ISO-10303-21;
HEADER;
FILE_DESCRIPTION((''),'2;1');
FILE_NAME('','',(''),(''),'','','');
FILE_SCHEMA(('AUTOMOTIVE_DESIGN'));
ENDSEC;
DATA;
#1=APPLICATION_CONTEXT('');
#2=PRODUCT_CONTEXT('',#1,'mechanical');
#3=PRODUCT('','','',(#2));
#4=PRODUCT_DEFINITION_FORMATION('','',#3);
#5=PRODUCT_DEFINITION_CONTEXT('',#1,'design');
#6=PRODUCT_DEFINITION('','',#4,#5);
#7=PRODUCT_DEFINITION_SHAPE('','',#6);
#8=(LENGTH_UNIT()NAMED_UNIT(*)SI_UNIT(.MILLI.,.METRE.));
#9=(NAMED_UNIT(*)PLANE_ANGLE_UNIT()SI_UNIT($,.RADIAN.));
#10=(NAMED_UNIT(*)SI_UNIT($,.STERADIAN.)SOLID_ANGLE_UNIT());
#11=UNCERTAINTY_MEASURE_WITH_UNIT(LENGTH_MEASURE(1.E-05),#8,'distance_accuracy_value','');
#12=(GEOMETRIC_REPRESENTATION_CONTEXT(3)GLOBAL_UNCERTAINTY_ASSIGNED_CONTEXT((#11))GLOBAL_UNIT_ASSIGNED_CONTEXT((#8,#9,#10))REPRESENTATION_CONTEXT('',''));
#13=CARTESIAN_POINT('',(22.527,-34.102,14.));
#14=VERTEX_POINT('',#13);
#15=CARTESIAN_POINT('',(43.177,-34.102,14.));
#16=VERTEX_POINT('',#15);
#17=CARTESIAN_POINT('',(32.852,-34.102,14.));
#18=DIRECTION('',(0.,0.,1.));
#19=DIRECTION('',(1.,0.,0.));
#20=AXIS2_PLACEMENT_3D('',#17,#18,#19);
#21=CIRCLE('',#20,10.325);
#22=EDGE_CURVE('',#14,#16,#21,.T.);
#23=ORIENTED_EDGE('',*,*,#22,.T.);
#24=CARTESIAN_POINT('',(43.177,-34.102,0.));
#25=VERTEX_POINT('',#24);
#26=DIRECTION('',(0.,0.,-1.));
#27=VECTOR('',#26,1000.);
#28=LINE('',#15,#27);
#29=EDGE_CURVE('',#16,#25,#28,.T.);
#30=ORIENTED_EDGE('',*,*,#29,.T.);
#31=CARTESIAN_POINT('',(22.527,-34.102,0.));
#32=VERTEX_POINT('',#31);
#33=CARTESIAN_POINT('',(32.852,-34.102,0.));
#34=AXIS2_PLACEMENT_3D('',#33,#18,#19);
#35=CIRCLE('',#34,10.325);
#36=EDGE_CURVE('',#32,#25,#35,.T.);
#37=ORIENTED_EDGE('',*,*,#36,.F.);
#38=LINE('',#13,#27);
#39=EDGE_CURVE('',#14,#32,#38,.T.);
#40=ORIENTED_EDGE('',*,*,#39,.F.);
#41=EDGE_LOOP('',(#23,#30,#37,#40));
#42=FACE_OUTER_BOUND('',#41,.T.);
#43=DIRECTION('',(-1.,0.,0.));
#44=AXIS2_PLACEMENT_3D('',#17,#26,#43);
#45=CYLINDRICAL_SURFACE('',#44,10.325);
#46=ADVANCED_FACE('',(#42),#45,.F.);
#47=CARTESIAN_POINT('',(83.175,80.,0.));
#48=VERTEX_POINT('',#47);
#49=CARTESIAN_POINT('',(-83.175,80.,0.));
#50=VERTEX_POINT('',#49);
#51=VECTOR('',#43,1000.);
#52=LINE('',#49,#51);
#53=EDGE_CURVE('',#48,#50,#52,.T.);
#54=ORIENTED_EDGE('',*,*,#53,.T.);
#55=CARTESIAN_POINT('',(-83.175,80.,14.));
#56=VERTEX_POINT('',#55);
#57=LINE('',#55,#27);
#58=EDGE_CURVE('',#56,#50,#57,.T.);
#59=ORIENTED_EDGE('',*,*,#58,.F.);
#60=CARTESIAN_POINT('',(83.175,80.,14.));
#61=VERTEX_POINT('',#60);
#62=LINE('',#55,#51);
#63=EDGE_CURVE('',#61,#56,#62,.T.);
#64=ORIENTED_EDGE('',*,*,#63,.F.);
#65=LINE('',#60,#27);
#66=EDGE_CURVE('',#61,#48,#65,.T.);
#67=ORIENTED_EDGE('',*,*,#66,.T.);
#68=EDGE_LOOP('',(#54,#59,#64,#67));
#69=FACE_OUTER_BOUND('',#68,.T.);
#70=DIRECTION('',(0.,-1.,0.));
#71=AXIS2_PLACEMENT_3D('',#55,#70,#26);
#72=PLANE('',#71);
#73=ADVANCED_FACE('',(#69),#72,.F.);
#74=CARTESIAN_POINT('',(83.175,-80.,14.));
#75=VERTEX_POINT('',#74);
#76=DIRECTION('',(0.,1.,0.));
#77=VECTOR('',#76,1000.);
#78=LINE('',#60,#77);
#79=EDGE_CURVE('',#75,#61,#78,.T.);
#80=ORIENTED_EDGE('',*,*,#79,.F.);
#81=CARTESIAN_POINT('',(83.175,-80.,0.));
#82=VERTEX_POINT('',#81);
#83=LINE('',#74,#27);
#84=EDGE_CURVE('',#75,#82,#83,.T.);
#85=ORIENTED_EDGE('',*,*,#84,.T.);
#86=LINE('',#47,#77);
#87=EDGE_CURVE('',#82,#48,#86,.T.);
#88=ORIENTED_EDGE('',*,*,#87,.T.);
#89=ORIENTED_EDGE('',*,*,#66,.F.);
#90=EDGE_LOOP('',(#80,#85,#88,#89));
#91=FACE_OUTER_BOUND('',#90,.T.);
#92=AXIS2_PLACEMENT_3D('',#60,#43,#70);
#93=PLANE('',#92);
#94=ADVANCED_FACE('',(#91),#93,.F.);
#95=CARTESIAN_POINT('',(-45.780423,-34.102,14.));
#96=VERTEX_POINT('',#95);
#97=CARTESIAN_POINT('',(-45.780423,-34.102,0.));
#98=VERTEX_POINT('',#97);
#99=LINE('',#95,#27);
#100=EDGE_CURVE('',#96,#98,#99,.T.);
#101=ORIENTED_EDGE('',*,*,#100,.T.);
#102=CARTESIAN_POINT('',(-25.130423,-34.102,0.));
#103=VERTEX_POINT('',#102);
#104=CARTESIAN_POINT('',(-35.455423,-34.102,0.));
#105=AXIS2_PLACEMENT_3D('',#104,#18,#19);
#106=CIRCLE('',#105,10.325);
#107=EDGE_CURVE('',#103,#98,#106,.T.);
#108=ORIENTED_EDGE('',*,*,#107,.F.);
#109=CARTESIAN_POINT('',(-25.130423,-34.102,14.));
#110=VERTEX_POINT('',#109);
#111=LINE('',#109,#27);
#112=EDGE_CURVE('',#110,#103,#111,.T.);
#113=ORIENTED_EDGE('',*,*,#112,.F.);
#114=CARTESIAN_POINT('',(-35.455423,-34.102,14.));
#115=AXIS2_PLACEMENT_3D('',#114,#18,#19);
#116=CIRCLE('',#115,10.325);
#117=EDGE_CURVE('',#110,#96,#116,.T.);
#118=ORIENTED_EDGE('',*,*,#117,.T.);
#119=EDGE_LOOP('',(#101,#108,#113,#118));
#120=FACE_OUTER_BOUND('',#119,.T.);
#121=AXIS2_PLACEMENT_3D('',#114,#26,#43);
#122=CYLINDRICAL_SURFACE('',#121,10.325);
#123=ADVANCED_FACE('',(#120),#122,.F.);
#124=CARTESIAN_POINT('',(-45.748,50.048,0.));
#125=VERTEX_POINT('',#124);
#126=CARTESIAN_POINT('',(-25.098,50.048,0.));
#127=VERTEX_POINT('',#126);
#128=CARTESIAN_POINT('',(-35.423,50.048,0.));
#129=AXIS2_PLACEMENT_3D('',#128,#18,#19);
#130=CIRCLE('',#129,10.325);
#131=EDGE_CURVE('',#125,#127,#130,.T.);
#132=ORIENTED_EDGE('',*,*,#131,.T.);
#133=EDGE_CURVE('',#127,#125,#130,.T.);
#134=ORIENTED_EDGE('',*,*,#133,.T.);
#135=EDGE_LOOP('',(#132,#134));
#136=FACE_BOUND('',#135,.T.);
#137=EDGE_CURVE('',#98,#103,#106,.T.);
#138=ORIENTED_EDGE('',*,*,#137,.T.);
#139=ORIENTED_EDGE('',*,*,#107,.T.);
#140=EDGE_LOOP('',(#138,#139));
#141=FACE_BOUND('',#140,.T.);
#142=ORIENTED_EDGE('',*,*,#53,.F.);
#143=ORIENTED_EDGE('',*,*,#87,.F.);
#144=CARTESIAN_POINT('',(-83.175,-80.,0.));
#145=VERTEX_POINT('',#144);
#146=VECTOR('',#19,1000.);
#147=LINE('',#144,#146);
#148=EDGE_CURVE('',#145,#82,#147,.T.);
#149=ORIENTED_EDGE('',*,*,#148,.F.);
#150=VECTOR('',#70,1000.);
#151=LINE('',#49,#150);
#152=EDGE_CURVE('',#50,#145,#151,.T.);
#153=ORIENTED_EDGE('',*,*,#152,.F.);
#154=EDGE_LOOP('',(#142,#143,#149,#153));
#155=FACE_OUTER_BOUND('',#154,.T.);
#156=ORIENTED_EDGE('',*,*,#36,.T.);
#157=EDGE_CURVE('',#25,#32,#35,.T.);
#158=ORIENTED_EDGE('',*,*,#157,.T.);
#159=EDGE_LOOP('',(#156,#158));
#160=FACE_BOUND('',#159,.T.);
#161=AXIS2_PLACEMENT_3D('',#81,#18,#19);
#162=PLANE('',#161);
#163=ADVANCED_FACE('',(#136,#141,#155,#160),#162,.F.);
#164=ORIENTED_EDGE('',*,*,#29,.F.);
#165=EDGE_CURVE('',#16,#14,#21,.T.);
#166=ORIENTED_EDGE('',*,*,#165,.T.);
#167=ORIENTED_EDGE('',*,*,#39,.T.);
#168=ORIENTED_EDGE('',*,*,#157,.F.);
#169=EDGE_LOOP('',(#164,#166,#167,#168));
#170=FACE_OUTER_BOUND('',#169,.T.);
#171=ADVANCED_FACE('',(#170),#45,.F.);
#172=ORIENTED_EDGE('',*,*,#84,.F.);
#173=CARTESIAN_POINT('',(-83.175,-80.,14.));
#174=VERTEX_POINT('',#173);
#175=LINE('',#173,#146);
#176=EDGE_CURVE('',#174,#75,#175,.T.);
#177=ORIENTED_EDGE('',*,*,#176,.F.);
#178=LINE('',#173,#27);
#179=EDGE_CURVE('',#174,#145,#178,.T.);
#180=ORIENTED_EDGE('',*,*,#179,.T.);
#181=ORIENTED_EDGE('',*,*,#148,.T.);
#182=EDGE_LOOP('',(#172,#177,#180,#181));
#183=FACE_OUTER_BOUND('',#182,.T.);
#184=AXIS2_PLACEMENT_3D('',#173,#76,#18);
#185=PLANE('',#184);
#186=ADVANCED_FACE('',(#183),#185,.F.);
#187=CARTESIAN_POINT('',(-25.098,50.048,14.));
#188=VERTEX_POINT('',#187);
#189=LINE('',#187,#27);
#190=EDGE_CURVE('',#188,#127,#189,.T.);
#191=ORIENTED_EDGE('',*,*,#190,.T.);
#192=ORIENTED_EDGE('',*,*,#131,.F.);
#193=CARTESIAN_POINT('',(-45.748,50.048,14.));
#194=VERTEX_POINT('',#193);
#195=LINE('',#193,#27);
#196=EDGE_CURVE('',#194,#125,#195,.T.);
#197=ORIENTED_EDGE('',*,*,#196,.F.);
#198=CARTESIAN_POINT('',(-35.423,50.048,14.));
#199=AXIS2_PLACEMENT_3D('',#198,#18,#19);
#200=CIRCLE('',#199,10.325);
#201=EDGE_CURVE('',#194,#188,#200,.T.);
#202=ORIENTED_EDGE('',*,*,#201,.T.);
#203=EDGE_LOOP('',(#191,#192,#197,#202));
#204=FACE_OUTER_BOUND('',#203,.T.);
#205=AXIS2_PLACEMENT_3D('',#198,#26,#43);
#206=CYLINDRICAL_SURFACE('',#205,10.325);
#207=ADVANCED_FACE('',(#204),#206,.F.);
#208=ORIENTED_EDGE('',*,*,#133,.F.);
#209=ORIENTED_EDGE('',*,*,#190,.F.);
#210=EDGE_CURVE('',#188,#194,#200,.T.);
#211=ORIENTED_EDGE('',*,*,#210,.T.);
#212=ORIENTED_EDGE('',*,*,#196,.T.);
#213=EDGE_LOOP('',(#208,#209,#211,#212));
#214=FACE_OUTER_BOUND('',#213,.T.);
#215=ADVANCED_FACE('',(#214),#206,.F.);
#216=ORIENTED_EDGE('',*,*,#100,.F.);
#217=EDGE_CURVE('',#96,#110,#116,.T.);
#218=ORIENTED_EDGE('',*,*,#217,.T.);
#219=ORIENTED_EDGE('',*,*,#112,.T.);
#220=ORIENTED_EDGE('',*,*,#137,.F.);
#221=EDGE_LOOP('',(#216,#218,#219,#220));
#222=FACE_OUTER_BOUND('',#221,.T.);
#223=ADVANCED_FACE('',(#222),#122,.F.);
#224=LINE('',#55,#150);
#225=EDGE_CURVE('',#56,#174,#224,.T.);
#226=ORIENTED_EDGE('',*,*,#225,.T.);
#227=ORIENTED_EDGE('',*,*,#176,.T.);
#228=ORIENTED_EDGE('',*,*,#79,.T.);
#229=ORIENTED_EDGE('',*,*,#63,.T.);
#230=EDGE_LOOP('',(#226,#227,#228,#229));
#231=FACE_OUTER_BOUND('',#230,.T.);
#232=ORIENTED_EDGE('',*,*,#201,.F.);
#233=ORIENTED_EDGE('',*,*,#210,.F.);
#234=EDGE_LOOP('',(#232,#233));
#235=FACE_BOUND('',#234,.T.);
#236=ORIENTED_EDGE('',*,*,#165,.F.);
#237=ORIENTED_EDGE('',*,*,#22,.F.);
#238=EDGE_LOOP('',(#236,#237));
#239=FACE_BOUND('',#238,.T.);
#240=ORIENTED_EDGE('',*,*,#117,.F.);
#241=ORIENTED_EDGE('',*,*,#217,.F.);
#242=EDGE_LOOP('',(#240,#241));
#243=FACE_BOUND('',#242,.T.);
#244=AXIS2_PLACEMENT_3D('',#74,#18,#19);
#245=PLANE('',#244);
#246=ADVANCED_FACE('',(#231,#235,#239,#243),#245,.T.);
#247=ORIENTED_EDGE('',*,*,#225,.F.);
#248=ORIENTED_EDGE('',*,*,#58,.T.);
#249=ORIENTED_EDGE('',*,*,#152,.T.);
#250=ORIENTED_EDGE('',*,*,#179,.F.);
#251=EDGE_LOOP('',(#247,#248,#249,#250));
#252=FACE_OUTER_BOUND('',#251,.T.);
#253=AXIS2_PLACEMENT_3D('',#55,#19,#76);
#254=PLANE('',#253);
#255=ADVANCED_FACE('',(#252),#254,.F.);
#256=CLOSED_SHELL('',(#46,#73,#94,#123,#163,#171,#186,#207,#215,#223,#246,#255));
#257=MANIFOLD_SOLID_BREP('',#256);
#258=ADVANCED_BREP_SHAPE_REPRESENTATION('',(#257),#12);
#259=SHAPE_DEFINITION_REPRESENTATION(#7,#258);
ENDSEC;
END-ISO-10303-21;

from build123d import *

# Parameters (mm, degrees)
SKETCH1_W           = 166.35
SKETCH1_H           = 160
SKETCH1_R           = 10.325
BOSS_EXTRUDE1_DEPTH = 14


with BuildPart() as part:
    # Sketch1 → Boss-Extrude1 (new body)
    with BuildSketch(Plane.XY):
        Rectangle(SKETCH1_W, SKETCH1_H)
        with Locations((-35.423, 50.048)):
            Circle(SKETCH1_R, mode=Mode.SUBTRACT)
        with Locations((-35.455423125, -34.102)):
            Circle(SKETCH1_R, mode=Mode.SUBTRACT)
        with Locations((32.852, -34.102)):
            Circle(SKETCH1_R, mode=Mode.SUBTRACT)
    extrude(amount=BOSS_EXTRUDE1_DEPTH)


solid = part.part
